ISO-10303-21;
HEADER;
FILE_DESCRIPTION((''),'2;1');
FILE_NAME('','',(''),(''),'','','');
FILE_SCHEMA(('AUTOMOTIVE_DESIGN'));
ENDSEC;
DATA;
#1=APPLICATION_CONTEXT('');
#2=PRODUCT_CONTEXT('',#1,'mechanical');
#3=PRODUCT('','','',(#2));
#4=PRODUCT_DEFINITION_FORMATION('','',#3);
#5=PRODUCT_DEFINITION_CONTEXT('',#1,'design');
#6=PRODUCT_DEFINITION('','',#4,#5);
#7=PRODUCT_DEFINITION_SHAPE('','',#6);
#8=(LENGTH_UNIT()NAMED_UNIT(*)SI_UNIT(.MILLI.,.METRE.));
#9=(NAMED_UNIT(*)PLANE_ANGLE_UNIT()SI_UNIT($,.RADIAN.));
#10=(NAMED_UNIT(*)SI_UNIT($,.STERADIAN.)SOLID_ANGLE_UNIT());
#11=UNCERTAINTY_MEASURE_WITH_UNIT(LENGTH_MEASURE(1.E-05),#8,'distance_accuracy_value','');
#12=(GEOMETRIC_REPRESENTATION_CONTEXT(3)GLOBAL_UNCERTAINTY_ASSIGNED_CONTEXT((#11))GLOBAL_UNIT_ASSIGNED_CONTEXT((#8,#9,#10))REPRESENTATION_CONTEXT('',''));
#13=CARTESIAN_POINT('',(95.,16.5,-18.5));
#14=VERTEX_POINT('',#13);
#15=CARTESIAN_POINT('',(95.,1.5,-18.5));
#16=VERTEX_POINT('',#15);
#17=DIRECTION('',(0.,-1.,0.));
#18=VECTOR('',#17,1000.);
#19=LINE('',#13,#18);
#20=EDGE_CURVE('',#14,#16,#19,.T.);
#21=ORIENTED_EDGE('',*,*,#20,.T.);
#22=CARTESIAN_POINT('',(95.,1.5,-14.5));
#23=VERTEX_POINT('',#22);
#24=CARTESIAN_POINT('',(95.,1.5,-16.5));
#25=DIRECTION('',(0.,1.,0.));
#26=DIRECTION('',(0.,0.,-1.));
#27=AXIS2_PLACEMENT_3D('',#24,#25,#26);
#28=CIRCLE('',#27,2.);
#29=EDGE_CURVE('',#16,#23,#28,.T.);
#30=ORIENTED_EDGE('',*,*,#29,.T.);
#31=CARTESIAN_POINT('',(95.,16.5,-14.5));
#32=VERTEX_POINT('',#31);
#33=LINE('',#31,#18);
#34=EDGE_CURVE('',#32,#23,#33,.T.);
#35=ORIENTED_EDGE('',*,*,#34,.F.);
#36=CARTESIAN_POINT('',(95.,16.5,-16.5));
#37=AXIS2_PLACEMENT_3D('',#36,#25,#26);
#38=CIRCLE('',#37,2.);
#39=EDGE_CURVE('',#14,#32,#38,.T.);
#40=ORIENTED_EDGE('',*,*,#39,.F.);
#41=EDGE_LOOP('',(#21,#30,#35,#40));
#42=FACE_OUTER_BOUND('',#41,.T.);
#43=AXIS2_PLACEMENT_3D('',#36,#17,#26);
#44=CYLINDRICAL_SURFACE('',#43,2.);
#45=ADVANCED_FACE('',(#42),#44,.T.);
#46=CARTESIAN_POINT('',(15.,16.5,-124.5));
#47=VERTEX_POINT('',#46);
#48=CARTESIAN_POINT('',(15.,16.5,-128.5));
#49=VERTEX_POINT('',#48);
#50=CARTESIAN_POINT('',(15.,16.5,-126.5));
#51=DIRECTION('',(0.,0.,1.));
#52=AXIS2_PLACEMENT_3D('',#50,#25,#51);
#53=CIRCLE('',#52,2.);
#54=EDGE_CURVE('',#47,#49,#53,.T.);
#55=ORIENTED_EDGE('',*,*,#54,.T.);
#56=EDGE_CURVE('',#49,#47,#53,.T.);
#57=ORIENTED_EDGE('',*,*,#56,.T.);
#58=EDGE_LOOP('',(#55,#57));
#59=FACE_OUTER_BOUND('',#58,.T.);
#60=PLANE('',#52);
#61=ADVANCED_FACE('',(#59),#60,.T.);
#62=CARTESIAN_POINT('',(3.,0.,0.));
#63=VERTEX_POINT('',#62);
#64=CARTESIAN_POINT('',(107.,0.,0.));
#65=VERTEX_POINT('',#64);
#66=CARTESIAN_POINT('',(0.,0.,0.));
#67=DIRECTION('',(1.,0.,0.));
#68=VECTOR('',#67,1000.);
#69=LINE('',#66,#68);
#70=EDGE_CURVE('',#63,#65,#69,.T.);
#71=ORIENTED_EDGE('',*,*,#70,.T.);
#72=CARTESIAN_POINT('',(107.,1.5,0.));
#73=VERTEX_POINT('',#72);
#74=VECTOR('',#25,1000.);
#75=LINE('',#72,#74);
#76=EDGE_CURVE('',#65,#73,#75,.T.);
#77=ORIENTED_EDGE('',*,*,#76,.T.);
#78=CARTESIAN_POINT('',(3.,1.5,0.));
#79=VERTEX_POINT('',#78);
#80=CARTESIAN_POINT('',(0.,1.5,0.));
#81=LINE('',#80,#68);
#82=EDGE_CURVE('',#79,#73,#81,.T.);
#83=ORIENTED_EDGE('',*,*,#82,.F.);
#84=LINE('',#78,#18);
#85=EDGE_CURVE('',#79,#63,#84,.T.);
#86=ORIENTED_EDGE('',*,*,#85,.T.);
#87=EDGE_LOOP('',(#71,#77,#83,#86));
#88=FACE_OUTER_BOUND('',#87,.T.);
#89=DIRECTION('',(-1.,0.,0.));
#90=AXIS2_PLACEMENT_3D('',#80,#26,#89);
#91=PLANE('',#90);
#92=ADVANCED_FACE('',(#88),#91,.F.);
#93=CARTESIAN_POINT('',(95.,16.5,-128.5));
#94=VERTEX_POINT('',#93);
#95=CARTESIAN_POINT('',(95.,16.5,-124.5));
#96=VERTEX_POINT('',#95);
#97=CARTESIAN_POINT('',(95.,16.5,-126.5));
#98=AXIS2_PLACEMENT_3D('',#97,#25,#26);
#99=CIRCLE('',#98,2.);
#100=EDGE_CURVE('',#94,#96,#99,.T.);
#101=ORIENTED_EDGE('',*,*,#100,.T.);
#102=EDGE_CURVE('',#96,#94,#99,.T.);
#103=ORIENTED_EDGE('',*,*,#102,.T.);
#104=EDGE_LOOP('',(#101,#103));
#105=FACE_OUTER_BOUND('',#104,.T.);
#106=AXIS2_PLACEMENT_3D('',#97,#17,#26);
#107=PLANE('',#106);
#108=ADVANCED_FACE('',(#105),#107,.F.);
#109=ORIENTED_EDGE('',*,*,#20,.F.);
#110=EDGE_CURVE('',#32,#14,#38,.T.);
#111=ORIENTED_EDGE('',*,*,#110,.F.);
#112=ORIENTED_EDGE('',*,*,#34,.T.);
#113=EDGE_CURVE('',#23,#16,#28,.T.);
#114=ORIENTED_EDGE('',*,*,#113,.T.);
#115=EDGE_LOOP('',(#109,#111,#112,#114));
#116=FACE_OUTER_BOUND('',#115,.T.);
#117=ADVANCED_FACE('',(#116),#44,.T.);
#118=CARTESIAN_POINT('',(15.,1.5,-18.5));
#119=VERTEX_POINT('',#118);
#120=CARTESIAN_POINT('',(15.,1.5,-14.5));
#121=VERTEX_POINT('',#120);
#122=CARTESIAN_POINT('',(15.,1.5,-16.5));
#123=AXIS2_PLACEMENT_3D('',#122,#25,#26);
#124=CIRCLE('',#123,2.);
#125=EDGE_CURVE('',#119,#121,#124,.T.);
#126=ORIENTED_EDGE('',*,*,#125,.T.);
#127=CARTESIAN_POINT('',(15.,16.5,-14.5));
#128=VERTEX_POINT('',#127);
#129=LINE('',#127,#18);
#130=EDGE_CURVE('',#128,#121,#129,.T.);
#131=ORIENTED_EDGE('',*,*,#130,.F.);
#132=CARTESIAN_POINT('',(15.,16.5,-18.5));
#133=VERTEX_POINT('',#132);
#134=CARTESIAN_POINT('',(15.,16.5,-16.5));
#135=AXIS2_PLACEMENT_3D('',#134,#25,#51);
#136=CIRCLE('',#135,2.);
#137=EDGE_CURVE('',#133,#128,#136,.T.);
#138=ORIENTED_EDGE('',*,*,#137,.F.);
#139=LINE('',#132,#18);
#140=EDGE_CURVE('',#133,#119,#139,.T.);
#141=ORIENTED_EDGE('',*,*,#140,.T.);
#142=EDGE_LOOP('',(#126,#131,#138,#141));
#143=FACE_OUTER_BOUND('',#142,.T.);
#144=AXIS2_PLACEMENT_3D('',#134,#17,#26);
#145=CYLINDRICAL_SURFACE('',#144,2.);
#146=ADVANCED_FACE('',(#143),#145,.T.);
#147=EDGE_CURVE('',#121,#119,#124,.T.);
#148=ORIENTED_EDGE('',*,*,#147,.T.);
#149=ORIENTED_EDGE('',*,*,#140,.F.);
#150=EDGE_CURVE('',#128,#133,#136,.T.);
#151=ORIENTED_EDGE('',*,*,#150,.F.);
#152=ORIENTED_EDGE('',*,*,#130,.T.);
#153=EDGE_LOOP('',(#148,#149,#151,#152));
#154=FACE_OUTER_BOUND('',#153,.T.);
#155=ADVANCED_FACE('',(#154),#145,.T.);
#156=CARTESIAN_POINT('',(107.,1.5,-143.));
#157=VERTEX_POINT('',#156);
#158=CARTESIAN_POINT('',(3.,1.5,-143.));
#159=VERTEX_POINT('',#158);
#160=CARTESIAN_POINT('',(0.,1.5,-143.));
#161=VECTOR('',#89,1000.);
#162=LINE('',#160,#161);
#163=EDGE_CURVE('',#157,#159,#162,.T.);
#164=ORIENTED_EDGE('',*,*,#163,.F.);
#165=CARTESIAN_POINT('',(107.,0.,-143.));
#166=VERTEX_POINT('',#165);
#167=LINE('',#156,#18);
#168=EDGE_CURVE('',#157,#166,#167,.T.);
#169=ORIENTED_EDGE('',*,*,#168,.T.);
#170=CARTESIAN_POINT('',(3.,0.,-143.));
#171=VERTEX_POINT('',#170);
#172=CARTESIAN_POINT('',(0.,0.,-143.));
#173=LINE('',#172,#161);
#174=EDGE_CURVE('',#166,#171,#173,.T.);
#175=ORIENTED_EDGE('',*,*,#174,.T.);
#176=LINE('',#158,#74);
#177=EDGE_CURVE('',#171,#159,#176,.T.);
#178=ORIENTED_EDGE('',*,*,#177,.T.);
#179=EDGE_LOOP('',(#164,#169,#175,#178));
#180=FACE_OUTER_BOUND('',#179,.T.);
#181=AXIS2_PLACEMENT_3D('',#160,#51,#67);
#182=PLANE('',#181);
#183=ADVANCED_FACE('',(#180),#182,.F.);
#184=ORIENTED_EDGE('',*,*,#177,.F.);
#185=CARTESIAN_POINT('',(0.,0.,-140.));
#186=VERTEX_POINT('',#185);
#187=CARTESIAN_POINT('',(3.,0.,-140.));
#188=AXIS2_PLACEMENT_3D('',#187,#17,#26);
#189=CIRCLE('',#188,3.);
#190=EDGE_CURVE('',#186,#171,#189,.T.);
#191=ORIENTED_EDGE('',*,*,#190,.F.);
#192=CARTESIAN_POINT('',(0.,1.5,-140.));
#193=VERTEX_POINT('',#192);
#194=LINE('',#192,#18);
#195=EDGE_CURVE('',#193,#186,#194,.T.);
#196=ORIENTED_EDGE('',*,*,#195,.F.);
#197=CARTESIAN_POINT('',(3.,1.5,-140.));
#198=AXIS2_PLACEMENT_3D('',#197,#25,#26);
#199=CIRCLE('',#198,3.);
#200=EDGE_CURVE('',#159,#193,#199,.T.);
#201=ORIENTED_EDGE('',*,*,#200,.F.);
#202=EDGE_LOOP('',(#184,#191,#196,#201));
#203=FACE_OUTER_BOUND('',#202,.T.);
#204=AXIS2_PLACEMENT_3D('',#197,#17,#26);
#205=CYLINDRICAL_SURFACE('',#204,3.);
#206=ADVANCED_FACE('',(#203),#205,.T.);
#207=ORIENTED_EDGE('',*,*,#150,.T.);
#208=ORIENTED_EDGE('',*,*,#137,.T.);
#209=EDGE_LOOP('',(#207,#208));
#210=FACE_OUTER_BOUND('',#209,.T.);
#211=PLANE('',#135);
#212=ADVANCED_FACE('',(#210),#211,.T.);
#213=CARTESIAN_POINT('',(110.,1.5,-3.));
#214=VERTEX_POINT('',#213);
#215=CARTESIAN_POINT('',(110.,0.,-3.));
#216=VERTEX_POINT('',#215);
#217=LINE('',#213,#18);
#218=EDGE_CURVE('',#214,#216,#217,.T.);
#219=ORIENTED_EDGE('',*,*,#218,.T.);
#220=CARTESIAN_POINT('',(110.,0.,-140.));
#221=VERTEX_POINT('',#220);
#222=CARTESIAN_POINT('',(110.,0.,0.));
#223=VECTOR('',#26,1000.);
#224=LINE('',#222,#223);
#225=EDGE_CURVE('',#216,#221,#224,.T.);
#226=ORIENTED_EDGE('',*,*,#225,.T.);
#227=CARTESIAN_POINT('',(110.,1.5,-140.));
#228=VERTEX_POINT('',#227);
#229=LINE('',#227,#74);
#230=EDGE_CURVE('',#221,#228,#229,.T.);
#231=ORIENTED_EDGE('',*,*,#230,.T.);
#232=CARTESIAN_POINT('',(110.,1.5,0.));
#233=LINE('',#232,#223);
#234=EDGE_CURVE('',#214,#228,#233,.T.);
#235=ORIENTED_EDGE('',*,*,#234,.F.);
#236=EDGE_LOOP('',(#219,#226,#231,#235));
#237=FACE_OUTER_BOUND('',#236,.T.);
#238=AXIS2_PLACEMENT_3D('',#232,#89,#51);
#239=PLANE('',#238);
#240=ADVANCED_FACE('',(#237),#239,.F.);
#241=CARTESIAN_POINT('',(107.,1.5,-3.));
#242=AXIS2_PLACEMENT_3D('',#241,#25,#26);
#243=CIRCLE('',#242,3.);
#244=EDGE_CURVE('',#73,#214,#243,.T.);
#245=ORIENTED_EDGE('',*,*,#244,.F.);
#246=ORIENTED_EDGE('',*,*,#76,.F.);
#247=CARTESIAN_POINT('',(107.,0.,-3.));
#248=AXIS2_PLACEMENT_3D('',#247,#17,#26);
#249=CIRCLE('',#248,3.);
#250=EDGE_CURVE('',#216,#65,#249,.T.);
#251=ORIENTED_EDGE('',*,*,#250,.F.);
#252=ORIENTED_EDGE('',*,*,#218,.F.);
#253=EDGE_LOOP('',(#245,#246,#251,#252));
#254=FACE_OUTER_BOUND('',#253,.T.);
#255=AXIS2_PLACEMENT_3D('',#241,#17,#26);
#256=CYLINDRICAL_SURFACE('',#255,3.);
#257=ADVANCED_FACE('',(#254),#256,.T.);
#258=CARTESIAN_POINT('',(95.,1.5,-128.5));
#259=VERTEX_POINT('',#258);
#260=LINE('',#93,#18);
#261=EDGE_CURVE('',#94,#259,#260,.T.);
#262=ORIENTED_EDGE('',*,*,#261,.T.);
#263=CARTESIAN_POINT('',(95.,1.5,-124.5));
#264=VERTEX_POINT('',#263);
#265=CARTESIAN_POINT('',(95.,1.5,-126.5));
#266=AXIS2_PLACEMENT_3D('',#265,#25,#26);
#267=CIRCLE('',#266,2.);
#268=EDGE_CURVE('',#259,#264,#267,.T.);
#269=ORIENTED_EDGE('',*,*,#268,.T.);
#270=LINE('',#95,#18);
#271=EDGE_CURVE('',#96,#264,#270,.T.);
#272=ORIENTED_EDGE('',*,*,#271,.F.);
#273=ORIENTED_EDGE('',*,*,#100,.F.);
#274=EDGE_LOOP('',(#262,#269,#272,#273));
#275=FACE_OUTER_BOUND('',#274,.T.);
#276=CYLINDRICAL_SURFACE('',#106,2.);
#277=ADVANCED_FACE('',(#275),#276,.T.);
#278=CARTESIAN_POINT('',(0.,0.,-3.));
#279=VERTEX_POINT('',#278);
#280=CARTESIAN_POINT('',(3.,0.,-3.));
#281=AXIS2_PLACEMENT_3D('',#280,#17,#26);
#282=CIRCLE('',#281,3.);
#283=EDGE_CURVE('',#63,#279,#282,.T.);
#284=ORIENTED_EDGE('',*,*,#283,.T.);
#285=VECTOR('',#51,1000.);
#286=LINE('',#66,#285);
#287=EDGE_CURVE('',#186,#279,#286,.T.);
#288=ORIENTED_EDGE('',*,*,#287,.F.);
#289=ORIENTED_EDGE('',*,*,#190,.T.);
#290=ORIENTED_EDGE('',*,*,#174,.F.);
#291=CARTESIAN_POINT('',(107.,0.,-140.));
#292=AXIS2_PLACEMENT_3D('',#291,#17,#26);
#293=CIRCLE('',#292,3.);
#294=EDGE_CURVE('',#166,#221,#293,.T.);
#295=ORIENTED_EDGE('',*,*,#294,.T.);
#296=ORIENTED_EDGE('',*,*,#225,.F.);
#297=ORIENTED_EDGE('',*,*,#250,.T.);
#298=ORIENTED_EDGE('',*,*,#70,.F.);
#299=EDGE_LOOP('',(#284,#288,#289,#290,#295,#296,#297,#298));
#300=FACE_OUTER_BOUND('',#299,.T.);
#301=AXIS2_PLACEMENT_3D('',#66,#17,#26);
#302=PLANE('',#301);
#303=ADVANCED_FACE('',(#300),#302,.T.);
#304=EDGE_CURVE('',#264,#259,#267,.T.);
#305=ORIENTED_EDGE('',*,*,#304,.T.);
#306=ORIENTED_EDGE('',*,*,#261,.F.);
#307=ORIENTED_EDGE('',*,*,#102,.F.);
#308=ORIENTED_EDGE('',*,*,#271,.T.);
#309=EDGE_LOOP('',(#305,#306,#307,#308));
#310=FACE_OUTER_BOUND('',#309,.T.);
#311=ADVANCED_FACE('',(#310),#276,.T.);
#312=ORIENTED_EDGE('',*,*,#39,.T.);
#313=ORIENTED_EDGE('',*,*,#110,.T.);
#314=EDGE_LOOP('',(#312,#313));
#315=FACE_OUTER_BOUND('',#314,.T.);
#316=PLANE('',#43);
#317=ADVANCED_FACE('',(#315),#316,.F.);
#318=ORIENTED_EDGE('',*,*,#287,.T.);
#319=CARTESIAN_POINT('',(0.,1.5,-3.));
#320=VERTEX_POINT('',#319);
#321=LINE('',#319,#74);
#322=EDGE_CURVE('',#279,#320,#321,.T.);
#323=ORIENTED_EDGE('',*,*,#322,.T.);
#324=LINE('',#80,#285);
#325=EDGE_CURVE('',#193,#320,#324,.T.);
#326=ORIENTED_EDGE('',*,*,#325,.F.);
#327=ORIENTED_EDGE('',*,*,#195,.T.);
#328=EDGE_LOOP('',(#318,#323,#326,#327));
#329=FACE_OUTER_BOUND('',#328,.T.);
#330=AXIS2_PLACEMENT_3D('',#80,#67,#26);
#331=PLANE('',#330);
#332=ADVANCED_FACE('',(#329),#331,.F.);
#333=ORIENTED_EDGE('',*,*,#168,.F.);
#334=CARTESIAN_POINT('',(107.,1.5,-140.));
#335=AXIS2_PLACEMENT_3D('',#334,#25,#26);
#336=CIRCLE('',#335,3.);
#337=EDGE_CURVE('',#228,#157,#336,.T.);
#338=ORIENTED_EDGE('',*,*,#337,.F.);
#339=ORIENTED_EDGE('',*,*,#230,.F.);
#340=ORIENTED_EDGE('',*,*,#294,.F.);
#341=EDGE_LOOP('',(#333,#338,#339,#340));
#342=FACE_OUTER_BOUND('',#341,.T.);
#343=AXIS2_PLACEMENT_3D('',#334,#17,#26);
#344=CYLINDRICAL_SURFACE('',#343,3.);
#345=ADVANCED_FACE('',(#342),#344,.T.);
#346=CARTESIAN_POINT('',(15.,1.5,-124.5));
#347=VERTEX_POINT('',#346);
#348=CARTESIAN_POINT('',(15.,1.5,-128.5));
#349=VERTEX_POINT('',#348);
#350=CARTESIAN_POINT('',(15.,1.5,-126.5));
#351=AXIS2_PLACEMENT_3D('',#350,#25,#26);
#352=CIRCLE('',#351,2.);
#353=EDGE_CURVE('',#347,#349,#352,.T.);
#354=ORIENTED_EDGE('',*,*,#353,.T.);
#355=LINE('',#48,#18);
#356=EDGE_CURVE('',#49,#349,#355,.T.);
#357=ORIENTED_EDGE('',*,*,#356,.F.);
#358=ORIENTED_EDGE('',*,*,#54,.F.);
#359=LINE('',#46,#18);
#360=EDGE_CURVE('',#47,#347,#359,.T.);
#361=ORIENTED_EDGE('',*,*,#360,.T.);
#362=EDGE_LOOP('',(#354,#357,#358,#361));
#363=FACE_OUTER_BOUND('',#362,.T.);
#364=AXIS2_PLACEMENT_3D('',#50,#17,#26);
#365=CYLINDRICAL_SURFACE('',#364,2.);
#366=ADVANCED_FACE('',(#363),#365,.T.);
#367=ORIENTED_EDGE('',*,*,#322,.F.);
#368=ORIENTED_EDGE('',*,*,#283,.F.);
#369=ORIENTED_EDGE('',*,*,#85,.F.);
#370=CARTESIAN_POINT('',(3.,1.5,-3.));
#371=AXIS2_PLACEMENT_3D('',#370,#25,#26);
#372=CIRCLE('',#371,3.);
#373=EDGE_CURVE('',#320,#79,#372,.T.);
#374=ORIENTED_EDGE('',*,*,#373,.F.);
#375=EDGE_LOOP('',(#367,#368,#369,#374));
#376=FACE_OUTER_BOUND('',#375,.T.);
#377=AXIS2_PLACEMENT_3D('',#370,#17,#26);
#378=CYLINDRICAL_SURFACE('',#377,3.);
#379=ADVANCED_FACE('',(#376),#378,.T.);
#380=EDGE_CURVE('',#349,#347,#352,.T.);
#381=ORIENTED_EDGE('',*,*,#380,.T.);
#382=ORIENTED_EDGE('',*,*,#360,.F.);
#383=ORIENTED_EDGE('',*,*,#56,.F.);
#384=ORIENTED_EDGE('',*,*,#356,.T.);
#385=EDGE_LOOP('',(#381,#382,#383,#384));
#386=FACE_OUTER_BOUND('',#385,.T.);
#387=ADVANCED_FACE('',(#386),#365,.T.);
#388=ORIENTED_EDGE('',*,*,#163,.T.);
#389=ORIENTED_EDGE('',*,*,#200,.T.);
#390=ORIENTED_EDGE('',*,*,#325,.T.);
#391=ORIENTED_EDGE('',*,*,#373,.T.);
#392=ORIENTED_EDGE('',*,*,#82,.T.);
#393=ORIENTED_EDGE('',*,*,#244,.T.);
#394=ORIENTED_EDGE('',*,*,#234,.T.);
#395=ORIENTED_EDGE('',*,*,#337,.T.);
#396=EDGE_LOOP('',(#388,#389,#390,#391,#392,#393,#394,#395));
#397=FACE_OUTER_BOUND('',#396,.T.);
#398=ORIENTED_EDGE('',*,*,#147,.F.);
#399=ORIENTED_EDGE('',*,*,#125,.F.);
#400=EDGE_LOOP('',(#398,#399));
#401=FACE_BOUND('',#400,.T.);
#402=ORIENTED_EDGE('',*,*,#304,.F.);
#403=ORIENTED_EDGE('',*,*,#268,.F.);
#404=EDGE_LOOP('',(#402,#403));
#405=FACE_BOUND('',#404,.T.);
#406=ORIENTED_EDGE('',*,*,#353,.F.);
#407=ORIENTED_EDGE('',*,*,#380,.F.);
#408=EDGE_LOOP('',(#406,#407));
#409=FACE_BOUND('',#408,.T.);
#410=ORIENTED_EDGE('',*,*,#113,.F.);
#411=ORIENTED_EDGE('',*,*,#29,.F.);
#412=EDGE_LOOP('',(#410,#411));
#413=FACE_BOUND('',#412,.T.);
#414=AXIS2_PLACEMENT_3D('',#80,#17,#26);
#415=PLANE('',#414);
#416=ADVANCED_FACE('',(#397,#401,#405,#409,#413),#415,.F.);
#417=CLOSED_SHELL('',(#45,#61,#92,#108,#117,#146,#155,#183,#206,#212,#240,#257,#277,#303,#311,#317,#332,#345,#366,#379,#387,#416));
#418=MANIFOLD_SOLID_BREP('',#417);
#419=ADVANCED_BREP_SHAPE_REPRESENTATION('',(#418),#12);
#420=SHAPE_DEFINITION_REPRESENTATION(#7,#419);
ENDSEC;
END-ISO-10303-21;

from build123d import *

# Parameters (mm, degrees)
SKETCH_1_W      = 110
SKETCH_1_H      = 143
EXTRUDE_1_DEPTH = 1.5
FILLET_1_R      = 3
SKETCH_2_R      = 2
EXTRUDE_2_DEPTH = 15


with BuildPart() as part:
    # 草图1 → 凸台-拉伸1 (new body)
    with BuildSketch(Plane(origin=(0, 0, 0), x_dir=(1, 0, 0), z_dir=(0, 1, 0))):
        with Locations((55, 71.5)):
            Rectangle(SKETCH_1_W, SKETCH_1_H)
    extrude(amount=EXTRUDE_1_DEPTH)

    # 圆角1
    fillet_1_edges = [part.edges().sort_by_distance(p)[0] for p in [
        (0, 0.75, -143),
        (110, 0.75, -143),
        (110, 0.75, 0),
        (0, 0.75, 0),
    ]]
    fillet(fillet_1_edges, radius=FILLET_1_R)

    # 草图2 → 凸台-拉伸2 (add)
    with BuildSketch(Plane(origin=(0, 1.5, 0), x_dir=(1, 0, 0), z_dir=(0, 1, 0))):
        with Locations(Location((15, 126.5, 0), (0, 0, 90))):
            Circle(SKETCH_2_R)
        with Locations(Location((95, 16.5, 0), (0, 0, 90))):
            Circle(SKETCH_2_R)
        with Locations(Location((15, 16.5, 0), (0, 0, 90))):
            Circle(SKETCH_2_R)
        with Locations(Location((95, 126.5, 0), (0, 0, 90))):
            Circle(SKETCH_2_R)
    extrude(amount=EXTRUDE_2_DEPTH)


solid = part.part
